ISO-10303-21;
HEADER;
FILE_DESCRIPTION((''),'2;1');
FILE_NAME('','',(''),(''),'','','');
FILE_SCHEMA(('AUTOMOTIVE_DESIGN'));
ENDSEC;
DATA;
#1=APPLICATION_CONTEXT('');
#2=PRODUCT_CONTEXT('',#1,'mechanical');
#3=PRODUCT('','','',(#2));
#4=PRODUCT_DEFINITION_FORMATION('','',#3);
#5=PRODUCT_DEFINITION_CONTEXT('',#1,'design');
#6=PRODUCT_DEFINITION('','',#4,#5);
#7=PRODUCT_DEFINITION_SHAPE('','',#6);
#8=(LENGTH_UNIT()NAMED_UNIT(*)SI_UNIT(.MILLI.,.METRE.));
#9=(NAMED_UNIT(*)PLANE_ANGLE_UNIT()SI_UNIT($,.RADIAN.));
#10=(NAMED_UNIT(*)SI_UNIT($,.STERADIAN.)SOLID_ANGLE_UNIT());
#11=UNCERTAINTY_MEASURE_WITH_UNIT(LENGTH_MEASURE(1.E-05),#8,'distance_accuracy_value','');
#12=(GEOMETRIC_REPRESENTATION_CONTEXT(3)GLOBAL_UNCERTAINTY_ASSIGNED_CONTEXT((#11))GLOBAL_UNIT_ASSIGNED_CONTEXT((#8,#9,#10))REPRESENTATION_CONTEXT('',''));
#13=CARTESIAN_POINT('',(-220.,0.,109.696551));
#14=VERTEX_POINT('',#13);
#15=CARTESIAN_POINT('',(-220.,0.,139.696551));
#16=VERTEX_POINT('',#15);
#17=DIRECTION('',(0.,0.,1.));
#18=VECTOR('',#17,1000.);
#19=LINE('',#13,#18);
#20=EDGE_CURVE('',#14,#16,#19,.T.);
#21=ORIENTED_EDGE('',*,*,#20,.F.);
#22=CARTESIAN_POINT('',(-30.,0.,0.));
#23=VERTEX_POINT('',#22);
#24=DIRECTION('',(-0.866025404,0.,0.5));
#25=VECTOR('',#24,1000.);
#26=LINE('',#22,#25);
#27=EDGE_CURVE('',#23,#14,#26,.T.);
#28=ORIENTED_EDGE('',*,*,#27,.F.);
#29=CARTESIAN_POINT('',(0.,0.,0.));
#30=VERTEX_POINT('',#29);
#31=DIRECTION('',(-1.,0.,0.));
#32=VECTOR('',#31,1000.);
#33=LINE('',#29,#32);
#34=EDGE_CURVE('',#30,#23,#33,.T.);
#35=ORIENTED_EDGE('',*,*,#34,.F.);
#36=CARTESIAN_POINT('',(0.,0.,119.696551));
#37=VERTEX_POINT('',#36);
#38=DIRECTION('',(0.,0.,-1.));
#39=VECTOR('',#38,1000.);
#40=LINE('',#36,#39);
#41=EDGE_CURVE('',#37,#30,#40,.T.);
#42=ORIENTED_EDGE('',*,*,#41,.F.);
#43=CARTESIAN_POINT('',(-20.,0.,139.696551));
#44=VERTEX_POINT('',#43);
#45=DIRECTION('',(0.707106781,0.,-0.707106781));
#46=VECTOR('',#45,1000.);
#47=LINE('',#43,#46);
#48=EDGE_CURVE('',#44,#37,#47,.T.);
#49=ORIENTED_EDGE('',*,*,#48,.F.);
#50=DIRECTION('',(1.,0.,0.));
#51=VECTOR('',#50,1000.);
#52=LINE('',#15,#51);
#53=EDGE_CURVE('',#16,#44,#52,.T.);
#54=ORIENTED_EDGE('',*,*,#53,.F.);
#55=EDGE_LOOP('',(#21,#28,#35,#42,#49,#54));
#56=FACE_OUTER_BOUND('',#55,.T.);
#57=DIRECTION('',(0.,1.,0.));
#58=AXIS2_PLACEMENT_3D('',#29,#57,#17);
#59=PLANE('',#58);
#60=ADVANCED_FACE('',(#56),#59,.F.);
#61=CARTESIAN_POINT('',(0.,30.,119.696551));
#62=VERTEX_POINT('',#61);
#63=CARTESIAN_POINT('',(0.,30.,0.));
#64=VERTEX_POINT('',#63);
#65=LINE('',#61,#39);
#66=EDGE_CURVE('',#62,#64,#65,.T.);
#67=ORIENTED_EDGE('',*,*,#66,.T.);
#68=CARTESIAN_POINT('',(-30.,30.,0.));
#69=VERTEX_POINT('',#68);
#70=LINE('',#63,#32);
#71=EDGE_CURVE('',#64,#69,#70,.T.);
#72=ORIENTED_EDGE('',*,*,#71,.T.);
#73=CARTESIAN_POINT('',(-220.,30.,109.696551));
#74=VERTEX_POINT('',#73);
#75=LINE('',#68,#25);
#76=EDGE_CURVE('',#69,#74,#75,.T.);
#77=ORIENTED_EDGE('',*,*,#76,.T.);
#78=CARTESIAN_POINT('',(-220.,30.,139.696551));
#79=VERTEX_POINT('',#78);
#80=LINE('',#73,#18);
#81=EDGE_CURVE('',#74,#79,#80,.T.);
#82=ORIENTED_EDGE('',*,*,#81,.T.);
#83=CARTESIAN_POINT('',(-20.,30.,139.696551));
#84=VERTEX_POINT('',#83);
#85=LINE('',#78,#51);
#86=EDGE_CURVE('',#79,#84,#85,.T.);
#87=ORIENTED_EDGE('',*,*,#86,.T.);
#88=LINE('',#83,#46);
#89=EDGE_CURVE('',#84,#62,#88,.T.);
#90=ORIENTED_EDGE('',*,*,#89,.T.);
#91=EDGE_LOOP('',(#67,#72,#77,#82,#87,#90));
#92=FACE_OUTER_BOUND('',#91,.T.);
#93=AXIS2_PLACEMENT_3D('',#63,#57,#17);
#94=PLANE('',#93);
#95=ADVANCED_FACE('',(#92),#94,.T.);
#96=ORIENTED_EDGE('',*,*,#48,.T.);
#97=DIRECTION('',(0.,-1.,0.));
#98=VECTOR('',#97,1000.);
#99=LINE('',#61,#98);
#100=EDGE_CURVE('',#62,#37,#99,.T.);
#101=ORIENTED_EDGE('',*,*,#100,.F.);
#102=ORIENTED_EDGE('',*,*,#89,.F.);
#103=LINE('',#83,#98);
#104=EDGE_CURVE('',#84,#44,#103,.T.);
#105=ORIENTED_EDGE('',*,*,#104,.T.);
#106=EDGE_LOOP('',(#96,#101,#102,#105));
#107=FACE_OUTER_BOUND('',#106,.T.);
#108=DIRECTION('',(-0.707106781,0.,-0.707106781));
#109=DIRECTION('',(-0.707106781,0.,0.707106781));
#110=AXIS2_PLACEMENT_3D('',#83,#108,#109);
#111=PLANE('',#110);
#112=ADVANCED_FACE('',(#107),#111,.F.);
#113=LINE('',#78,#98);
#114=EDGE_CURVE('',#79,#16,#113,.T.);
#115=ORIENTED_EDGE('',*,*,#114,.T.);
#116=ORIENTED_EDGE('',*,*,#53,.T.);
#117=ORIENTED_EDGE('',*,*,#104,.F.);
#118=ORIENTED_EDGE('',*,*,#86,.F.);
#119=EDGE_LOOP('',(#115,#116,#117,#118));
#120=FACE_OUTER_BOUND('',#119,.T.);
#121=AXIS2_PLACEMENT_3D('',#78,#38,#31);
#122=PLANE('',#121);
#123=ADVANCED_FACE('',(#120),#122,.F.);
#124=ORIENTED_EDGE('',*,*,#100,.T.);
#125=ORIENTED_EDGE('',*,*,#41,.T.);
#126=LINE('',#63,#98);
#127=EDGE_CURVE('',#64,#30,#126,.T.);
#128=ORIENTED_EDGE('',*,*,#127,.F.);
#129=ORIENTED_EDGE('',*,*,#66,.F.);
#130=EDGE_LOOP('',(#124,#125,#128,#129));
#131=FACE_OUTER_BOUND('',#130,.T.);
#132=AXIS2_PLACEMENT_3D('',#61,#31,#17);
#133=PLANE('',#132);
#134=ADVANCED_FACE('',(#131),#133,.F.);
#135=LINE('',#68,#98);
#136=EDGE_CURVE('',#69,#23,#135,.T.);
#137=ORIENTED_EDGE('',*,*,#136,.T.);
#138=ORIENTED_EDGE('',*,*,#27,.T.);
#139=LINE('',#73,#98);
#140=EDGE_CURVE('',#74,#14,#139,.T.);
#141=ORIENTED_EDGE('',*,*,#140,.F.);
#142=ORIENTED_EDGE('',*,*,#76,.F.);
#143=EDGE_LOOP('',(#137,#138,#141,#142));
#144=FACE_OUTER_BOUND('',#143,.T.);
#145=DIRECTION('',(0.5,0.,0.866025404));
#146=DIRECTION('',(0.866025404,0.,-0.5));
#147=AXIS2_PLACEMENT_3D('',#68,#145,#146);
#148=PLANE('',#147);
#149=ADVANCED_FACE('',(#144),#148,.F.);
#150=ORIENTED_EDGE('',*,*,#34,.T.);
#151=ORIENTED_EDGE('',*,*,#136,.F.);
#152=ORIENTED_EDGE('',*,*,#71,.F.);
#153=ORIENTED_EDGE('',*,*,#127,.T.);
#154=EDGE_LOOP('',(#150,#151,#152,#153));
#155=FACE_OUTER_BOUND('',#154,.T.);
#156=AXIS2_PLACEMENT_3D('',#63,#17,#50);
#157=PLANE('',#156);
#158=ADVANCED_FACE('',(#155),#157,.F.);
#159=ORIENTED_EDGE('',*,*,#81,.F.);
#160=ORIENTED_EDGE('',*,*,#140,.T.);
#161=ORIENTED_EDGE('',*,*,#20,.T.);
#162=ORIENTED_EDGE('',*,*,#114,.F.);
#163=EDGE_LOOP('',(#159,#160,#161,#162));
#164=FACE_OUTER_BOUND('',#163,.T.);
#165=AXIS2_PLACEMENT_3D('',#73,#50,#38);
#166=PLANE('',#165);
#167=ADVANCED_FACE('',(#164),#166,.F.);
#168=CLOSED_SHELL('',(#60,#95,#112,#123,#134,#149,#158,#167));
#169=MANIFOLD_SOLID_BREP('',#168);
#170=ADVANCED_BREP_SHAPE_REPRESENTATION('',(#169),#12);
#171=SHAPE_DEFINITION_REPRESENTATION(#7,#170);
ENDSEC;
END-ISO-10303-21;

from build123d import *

# Parameters (mm, degrees)
EXTRUDE_1_DEPTH = 30


with BuildPart() as part:
    # 草图1 → 凸台-拉伸1 (new body)
    with BuildSketch(Plane(origin=(0, 0, 0), x_dir=(1, 0, 0), z_dir=(0, 1, 0))):
        Polygon((0, 0), (-30, 0), (-220, -109.696551146), (-220, -139.696551146), (-20, -139.696551146), (0, -119.696551146), align=None)
    extrude(amount=EXTRUDE_1_DEPTH)


solid = part.part
